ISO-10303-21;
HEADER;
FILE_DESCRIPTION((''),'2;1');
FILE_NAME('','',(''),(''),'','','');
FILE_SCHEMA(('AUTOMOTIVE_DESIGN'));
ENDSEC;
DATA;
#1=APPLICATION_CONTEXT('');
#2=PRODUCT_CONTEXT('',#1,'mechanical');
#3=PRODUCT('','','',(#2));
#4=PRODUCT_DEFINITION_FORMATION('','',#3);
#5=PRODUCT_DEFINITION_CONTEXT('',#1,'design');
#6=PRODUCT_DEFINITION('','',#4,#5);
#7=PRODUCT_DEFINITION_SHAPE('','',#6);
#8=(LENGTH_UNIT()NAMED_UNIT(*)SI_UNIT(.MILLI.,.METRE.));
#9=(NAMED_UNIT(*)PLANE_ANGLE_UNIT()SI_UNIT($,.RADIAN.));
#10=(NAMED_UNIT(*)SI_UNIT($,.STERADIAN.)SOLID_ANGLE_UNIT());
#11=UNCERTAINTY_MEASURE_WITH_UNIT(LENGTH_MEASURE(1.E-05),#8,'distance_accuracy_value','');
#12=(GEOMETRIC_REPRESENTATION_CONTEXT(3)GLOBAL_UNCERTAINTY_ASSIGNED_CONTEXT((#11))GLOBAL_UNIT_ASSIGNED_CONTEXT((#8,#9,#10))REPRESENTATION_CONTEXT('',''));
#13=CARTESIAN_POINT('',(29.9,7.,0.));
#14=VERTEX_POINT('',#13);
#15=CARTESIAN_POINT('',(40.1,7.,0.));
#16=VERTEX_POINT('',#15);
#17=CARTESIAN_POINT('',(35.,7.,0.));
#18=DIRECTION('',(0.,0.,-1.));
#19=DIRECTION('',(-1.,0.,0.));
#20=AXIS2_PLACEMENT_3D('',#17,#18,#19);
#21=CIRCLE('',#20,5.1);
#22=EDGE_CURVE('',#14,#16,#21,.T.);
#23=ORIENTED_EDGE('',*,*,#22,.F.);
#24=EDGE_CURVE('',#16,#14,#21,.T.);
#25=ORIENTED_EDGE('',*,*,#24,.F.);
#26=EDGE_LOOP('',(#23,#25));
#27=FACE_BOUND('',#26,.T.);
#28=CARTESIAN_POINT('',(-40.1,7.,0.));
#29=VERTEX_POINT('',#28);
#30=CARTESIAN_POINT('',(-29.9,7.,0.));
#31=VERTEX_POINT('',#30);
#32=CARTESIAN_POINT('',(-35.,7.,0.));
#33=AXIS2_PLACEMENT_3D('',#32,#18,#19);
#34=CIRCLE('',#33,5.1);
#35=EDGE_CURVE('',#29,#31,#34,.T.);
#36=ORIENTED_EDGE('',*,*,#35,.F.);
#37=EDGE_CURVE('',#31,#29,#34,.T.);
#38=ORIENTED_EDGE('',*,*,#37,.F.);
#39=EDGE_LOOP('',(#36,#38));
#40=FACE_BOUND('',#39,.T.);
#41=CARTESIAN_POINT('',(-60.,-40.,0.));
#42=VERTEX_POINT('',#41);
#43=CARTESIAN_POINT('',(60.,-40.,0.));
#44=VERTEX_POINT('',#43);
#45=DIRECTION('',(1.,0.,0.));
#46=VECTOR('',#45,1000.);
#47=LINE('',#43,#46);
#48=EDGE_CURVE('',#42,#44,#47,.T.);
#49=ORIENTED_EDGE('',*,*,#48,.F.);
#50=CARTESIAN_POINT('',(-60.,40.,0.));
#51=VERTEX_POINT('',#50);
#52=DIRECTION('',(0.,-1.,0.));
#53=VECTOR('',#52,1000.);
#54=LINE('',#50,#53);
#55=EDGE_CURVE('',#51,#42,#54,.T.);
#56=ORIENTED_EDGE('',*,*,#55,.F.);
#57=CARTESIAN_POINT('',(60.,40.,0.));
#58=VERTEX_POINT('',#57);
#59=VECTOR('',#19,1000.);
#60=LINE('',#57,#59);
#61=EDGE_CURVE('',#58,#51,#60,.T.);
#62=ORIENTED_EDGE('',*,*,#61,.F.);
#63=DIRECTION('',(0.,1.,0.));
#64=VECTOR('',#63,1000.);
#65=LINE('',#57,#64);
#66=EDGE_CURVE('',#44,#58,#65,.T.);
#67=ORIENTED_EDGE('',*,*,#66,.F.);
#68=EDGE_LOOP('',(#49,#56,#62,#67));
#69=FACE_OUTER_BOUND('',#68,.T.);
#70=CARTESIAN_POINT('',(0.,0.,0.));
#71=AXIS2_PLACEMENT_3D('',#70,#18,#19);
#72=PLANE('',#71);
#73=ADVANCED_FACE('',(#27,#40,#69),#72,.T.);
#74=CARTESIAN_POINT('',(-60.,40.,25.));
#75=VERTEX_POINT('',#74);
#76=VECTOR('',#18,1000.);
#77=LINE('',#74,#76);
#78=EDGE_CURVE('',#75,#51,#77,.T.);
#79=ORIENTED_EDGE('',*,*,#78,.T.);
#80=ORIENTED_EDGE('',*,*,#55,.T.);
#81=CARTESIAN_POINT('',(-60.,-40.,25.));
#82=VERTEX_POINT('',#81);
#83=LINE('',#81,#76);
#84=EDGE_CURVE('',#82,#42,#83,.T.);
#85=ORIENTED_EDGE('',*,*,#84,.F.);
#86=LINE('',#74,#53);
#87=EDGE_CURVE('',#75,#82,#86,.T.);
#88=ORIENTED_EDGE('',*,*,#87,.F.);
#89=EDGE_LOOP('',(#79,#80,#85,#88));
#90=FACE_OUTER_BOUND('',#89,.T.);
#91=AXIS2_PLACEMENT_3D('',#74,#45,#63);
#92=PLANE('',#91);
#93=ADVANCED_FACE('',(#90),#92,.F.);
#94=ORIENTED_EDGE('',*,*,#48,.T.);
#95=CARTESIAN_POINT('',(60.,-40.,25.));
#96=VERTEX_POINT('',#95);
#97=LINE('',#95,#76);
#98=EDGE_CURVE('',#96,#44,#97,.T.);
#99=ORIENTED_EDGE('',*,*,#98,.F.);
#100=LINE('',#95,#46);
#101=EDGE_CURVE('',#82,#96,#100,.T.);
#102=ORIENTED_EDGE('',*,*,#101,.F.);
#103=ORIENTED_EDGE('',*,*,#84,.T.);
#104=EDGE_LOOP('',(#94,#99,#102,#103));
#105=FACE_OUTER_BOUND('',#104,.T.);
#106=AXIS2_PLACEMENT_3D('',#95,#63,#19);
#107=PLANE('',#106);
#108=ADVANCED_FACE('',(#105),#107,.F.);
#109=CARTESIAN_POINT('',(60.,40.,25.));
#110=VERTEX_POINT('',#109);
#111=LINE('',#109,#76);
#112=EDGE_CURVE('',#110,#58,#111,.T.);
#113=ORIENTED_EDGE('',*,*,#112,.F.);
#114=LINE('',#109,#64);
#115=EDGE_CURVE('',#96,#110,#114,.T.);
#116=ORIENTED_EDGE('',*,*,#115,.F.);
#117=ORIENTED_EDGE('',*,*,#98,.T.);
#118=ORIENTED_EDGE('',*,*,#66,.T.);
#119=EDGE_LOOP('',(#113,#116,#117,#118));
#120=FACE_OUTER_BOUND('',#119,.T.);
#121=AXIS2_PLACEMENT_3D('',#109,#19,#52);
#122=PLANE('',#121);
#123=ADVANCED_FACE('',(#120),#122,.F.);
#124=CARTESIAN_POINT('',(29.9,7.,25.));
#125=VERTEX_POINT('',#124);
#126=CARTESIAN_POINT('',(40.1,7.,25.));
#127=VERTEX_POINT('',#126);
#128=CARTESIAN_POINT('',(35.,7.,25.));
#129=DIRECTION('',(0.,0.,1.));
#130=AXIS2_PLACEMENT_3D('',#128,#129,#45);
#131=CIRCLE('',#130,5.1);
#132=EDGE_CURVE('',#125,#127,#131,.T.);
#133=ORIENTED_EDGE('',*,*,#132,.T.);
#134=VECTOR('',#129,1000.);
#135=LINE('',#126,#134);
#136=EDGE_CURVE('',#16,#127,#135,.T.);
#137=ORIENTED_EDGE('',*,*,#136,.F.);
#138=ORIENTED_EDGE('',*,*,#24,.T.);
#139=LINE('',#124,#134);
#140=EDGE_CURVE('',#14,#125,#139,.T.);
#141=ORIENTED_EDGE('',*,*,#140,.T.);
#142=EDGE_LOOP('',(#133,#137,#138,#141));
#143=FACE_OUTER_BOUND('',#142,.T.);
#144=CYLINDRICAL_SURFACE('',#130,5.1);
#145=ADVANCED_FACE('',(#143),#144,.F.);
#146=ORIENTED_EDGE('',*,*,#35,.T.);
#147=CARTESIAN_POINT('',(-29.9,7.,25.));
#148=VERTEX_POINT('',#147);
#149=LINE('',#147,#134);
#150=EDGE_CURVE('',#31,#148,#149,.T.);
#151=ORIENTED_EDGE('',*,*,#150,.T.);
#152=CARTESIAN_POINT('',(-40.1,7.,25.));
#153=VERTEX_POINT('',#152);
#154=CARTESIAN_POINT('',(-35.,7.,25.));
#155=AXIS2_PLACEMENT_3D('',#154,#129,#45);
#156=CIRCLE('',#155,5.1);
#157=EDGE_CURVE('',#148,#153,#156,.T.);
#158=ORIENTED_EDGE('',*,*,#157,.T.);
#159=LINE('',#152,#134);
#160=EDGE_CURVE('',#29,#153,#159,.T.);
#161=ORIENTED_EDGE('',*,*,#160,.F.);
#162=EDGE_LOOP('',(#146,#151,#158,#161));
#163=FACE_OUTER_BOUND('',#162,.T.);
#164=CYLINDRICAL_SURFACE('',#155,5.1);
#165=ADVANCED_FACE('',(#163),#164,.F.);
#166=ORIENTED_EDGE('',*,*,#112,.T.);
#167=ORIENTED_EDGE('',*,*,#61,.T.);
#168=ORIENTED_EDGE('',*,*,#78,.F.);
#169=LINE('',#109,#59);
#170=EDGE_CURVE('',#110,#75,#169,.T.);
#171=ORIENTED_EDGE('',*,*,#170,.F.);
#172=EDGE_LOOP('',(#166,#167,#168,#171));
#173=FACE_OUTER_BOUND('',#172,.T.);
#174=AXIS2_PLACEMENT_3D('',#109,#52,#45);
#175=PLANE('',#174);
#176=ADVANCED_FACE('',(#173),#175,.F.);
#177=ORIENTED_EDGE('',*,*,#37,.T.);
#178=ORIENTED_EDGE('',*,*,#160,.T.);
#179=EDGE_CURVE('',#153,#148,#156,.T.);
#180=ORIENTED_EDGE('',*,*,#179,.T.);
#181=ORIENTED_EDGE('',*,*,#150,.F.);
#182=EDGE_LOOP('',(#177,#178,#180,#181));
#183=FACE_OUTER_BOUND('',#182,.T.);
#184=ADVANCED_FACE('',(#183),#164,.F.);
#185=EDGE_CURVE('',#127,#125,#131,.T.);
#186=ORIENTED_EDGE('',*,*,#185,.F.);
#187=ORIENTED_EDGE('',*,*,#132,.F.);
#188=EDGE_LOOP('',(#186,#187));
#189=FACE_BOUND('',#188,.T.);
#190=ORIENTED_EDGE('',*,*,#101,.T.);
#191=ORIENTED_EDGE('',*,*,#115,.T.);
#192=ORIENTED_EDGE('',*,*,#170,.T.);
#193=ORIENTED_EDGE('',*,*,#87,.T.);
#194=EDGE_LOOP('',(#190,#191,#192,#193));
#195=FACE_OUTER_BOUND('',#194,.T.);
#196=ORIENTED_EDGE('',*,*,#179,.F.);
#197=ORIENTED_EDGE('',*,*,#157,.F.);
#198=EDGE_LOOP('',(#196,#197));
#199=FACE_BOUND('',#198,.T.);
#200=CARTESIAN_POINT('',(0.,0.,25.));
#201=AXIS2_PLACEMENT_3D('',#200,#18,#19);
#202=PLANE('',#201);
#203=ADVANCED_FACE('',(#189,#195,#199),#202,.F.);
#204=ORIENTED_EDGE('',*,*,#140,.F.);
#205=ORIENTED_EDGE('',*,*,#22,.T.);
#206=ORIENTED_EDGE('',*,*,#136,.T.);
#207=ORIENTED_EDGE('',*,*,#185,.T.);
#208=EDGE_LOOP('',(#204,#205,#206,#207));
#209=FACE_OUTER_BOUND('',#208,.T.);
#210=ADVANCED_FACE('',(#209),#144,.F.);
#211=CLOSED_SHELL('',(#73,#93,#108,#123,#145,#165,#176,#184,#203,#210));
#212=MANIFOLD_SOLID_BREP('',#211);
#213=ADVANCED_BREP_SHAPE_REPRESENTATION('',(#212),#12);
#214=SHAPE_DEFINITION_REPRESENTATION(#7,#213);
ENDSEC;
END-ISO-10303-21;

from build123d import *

# Parameters (mm, degrees)
SKETCH1_W              = 120
SKETCH1_H              = 80
BOSS_EXTRUDE1_DEPTH    = 25
M12_TAPPED_HOLE1_D     = 10.2
M12_TAPPED_HOLE1_DEPTH = 29.25
M12_TAPPED_HOLE1_TIP   = 3.064389157


with BuildPart() as part:
    # Sketch1 → Boss-Extrude1 (new body)
    with BuildSketch(Plane.XY):
        Rectangle(SKETCH1_W, SKETCH1_H)
    extrude(amount=BOSS_EXTRUDE1_DEPTH)

    # M12 Tapped Hole1
    with Locations(Plane.XY.offset(25)):
        with Locations((-35, 7), (35, 7)):
            Hole(M12_TAPPED_HOLE1_D / 2, depth=M12_TAPPED_HOLE1_DEPTH)
            with Locations((0, 0, -(M12_TAPPED_HOLE1_DEPTH + M12_TAPPED_HOLE1_TIP / 2))):  # 118° drill point
                Cone(0, M12_TAPPED_HOLE1_D / 2, M12_TAPPED_HOLE1_TIP, mode=Mode.SUBTRACT)


solid = part.part
